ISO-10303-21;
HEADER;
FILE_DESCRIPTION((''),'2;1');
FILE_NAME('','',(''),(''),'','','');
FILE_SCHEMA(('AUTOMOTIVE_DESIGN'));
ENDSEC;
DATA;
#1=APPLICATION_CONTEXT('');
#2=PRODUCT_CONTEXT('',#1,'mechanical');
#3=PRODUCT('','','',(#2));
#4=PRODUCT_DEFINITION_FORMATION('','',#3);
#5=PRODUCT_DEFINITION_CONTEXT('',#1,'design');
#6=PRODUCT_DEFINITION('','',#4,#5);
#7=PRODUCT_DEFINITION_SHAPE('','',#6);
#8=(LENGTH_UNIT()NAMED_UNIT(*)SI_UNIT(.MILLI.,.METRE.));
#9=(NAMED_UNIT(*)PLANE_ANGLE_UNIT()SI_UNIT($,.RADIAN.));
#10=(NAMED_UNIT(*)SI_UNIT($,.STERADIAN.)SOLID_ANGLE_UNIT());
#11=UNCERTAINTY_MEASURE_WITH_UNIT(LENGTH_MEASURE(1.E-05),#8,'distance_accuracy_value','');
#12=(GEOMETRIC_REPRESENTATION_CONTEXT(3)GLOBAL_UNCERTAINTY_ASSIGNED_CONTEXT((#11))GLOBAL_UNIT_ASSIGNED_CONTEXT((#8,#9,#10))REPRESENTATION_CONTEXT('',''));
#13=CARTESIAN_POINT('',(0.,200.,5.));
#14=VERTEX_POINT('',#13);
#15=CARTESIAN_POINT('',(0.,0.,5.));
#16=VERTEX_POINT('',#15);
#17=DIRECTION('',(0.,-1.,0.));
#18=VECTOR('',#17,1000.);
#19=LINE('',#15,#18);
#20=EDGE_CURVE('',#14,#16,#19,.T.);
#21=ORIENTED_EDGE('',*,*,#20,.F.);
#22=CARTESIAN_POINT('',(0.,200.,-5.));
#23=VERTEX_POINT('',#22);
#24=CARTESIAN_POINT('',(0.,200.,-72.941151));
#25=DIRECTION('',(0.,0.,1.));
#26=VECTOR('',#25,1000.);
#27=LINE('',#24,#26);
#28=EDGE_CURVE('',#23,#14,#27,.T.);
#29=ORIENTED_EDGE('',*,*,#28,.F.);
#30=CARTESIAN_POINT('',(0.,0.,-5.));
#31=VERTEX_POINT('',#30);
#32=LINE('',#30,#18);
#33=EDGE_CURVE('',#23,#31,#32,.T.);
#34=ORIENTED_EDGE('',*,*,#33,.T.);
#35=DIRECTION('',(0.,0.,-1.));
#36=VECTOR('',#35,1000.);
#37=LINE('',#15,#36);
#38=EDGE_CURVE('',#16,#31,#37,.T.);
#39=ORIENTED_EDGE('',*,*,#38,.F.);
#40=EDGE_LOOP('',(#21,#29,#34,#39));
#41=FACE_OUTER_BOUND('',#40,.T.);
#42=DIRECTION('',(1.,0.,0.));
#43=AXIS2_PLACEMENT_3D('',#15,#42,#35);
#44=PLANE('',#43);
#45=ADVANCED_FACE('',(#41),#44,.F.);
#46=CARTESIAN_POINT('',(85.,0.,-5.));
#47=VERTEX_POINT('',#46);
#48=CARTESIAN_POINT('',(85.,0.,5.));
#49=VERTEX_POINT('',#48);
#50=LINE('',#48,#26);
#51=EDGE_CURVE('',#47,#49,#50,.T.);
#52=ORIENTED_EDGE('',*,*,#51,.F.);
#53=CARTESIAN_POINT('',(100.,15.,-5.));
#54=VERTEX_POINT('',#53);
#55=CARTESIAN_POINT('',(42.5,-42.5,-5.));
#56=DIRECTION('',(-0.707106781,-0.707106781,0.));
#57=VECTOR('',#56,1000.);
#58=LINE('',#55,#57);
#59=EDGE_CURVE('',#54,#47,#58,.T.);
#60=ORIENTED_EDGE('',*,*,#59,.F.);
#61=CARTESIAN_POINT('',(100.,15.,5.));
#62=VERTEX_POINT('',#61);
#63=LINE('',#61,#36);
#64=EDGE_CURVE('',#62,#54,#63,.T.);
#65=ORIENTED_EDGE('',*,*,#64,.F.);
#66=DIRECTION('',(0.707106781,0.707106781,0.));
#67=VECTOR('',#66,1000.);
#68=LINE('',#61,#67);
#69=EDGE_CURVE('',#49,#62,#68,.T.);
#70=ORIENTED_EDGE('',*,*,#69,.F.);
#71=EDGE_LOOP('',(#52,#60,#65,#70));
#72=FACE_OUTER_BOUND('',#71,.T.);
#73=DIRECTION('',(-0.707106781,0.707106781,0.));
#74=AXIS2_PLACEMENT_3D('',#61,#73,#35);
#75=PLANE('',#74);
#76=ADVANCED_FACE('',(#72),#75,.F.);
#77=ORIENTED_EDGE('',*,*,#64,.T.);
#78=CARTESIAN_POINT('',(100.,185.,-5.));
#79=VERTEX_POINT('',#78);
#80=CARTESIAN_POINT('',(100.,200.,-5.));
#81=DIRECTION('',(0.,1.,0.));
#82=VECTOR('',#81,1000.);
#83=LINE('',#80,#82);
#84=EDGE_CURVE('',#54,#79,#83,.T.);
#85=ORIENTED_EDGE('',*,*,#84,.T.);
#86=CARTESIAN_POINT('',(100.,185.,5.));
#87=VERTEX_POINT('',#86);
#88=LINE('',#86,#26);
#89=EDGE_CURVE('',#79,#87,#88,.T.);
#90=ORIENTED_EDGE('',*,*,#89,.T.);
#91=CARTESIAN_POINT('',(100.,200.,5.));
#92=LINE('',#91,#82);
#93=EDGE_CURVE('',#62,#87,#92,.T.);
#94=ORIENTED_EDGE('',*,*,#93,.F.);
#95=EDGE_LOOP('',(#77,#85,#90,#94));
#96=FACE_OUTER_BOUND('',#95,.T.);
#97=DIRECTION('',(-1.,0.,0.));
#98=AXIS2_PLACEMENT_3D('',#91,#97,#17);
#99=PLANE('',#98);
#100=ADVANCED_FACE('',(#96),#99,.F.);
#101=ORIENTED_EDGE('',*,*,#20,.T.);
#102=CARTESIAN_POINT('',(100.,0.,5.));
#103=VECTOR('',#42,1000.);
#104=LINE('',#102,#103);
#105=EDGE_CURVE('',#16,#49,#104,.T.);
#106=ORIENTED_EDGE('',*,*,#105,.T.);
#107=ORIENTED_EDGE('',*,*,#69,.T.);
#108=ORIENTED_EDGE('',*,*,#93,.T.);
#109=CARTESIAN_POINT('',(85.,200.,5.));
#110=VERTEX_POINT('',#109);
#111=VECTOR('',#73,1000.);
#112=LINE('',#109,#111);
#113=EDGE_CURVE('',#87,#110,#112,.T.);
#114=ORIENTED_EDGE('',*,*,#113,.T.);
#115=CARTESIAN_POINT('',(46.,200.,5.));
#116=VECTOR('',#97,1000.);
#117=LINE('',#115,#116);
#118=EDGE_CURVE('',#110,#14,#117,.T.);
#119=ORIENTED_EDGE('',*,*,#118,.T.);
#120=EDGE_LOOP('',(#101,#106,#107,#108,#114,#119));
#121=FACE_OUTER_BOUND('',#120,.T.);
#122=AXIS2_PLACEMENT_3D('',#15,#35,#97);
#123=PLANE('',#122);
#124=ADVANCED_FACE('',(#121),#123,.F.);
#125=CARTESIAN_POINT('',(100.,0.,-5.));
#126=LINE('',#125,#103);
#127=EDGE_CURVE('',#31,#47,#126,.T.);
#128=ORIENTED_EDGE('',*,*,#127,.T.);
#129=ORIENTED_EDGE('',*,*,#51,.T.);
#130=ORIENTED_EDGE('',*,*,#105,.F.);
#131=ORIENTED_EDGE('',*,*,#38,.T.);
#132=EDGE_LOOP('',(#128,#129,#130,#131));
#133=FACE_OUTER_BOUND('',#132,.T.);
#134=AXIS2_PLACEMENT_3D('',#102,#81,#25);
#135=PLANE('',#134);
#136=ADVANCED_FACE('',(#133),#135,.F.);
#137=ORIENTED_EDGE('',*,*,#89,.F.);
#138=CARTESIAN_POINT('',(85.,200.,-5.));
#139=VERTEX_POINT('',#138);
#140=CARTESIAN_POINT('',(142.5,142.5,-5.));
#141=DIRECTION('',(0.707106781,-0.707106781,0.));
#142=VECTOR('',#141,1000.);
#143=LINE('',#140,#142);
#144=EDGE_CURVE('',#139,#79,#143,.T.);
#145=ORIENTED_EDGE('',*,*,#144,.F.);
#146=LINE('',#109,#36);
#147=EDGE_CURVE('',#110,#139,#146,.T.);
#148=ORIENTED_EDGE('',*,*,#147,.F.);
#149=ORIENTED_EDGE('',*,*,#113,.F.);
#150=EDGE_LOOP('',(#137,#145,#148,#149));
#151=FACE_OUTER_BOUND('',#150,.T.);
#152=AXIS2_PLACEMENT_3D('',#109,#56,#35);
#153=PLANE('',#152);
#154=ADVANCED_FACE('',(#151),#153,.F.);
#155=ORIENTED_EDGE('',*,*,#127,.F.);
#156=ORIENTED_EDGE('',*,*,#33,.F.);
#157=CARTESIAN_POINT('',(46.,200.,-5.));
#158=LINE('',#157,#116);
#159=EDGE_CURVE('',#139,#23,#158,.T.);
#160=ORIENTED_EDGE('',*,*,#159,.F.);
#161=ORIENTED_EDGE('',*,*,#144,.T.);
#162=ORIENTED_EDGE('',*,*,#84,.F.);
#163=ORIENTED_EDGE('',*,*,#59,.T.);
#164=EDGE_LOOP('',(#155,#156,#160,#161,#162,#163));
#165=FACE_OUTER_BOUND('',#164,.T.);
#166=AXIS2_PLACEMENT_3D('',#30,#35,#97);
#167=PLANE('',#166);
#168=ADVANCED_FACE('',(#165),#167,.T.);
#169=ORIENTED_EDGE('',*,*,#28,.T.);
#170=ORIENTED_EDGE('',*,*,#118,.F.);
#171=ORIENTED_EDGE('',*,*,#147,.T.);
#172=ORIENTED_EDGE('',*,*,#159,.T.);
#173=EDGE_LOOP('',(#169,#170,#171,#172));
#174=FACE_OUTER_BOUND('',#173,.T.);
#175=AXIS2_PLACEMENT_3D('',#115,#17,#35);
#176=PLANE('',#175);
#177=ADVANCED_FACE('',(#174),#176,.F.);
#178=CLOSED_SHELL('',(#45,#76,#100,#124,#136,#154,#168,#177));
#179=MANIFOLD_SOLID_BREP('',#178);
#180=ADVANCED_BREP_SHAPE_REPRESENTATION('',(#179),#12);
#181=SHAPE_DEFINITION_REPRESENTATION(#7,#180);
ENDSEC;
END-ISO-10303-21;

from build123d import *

# Parameters (mm, degrees)
EXTRUDE_1_DEPTH = 5
CHAMFER_1_SIZE  = 15
EXTRUDE_2_DEPTH = 10


with BuildPart() as part:
    # 草图1 → 凸台-拉伸1 (new, symmetric)
    with BuildSketch(Plane.XY):
        Polygon((0, 0), (0, 150), (46, 200), (100, 200), (100, 0), align=None)
    extrude(amount=EXTRUDE_1_DEPTH, both=True)

    # 倒角1
    chamfer_1_edges = [part.edges().sort_by_distance(p)[0] for p in [
        (100, 200, 0),
        (100, 0, 0),
    ]]
    chamfer(chamfer_1_edges, length=CHAMFER_1_SIZE)

    # 草图2 → 凸台-拉伸2 (add)
    with BuildSketch(Plane.XY.offset(5)):
        Polygon((0, 150), (0, 200), (46, 200), align=None)
    extrude(amount=-EXTRUDE_2_DEPTH)


solid = part.part
